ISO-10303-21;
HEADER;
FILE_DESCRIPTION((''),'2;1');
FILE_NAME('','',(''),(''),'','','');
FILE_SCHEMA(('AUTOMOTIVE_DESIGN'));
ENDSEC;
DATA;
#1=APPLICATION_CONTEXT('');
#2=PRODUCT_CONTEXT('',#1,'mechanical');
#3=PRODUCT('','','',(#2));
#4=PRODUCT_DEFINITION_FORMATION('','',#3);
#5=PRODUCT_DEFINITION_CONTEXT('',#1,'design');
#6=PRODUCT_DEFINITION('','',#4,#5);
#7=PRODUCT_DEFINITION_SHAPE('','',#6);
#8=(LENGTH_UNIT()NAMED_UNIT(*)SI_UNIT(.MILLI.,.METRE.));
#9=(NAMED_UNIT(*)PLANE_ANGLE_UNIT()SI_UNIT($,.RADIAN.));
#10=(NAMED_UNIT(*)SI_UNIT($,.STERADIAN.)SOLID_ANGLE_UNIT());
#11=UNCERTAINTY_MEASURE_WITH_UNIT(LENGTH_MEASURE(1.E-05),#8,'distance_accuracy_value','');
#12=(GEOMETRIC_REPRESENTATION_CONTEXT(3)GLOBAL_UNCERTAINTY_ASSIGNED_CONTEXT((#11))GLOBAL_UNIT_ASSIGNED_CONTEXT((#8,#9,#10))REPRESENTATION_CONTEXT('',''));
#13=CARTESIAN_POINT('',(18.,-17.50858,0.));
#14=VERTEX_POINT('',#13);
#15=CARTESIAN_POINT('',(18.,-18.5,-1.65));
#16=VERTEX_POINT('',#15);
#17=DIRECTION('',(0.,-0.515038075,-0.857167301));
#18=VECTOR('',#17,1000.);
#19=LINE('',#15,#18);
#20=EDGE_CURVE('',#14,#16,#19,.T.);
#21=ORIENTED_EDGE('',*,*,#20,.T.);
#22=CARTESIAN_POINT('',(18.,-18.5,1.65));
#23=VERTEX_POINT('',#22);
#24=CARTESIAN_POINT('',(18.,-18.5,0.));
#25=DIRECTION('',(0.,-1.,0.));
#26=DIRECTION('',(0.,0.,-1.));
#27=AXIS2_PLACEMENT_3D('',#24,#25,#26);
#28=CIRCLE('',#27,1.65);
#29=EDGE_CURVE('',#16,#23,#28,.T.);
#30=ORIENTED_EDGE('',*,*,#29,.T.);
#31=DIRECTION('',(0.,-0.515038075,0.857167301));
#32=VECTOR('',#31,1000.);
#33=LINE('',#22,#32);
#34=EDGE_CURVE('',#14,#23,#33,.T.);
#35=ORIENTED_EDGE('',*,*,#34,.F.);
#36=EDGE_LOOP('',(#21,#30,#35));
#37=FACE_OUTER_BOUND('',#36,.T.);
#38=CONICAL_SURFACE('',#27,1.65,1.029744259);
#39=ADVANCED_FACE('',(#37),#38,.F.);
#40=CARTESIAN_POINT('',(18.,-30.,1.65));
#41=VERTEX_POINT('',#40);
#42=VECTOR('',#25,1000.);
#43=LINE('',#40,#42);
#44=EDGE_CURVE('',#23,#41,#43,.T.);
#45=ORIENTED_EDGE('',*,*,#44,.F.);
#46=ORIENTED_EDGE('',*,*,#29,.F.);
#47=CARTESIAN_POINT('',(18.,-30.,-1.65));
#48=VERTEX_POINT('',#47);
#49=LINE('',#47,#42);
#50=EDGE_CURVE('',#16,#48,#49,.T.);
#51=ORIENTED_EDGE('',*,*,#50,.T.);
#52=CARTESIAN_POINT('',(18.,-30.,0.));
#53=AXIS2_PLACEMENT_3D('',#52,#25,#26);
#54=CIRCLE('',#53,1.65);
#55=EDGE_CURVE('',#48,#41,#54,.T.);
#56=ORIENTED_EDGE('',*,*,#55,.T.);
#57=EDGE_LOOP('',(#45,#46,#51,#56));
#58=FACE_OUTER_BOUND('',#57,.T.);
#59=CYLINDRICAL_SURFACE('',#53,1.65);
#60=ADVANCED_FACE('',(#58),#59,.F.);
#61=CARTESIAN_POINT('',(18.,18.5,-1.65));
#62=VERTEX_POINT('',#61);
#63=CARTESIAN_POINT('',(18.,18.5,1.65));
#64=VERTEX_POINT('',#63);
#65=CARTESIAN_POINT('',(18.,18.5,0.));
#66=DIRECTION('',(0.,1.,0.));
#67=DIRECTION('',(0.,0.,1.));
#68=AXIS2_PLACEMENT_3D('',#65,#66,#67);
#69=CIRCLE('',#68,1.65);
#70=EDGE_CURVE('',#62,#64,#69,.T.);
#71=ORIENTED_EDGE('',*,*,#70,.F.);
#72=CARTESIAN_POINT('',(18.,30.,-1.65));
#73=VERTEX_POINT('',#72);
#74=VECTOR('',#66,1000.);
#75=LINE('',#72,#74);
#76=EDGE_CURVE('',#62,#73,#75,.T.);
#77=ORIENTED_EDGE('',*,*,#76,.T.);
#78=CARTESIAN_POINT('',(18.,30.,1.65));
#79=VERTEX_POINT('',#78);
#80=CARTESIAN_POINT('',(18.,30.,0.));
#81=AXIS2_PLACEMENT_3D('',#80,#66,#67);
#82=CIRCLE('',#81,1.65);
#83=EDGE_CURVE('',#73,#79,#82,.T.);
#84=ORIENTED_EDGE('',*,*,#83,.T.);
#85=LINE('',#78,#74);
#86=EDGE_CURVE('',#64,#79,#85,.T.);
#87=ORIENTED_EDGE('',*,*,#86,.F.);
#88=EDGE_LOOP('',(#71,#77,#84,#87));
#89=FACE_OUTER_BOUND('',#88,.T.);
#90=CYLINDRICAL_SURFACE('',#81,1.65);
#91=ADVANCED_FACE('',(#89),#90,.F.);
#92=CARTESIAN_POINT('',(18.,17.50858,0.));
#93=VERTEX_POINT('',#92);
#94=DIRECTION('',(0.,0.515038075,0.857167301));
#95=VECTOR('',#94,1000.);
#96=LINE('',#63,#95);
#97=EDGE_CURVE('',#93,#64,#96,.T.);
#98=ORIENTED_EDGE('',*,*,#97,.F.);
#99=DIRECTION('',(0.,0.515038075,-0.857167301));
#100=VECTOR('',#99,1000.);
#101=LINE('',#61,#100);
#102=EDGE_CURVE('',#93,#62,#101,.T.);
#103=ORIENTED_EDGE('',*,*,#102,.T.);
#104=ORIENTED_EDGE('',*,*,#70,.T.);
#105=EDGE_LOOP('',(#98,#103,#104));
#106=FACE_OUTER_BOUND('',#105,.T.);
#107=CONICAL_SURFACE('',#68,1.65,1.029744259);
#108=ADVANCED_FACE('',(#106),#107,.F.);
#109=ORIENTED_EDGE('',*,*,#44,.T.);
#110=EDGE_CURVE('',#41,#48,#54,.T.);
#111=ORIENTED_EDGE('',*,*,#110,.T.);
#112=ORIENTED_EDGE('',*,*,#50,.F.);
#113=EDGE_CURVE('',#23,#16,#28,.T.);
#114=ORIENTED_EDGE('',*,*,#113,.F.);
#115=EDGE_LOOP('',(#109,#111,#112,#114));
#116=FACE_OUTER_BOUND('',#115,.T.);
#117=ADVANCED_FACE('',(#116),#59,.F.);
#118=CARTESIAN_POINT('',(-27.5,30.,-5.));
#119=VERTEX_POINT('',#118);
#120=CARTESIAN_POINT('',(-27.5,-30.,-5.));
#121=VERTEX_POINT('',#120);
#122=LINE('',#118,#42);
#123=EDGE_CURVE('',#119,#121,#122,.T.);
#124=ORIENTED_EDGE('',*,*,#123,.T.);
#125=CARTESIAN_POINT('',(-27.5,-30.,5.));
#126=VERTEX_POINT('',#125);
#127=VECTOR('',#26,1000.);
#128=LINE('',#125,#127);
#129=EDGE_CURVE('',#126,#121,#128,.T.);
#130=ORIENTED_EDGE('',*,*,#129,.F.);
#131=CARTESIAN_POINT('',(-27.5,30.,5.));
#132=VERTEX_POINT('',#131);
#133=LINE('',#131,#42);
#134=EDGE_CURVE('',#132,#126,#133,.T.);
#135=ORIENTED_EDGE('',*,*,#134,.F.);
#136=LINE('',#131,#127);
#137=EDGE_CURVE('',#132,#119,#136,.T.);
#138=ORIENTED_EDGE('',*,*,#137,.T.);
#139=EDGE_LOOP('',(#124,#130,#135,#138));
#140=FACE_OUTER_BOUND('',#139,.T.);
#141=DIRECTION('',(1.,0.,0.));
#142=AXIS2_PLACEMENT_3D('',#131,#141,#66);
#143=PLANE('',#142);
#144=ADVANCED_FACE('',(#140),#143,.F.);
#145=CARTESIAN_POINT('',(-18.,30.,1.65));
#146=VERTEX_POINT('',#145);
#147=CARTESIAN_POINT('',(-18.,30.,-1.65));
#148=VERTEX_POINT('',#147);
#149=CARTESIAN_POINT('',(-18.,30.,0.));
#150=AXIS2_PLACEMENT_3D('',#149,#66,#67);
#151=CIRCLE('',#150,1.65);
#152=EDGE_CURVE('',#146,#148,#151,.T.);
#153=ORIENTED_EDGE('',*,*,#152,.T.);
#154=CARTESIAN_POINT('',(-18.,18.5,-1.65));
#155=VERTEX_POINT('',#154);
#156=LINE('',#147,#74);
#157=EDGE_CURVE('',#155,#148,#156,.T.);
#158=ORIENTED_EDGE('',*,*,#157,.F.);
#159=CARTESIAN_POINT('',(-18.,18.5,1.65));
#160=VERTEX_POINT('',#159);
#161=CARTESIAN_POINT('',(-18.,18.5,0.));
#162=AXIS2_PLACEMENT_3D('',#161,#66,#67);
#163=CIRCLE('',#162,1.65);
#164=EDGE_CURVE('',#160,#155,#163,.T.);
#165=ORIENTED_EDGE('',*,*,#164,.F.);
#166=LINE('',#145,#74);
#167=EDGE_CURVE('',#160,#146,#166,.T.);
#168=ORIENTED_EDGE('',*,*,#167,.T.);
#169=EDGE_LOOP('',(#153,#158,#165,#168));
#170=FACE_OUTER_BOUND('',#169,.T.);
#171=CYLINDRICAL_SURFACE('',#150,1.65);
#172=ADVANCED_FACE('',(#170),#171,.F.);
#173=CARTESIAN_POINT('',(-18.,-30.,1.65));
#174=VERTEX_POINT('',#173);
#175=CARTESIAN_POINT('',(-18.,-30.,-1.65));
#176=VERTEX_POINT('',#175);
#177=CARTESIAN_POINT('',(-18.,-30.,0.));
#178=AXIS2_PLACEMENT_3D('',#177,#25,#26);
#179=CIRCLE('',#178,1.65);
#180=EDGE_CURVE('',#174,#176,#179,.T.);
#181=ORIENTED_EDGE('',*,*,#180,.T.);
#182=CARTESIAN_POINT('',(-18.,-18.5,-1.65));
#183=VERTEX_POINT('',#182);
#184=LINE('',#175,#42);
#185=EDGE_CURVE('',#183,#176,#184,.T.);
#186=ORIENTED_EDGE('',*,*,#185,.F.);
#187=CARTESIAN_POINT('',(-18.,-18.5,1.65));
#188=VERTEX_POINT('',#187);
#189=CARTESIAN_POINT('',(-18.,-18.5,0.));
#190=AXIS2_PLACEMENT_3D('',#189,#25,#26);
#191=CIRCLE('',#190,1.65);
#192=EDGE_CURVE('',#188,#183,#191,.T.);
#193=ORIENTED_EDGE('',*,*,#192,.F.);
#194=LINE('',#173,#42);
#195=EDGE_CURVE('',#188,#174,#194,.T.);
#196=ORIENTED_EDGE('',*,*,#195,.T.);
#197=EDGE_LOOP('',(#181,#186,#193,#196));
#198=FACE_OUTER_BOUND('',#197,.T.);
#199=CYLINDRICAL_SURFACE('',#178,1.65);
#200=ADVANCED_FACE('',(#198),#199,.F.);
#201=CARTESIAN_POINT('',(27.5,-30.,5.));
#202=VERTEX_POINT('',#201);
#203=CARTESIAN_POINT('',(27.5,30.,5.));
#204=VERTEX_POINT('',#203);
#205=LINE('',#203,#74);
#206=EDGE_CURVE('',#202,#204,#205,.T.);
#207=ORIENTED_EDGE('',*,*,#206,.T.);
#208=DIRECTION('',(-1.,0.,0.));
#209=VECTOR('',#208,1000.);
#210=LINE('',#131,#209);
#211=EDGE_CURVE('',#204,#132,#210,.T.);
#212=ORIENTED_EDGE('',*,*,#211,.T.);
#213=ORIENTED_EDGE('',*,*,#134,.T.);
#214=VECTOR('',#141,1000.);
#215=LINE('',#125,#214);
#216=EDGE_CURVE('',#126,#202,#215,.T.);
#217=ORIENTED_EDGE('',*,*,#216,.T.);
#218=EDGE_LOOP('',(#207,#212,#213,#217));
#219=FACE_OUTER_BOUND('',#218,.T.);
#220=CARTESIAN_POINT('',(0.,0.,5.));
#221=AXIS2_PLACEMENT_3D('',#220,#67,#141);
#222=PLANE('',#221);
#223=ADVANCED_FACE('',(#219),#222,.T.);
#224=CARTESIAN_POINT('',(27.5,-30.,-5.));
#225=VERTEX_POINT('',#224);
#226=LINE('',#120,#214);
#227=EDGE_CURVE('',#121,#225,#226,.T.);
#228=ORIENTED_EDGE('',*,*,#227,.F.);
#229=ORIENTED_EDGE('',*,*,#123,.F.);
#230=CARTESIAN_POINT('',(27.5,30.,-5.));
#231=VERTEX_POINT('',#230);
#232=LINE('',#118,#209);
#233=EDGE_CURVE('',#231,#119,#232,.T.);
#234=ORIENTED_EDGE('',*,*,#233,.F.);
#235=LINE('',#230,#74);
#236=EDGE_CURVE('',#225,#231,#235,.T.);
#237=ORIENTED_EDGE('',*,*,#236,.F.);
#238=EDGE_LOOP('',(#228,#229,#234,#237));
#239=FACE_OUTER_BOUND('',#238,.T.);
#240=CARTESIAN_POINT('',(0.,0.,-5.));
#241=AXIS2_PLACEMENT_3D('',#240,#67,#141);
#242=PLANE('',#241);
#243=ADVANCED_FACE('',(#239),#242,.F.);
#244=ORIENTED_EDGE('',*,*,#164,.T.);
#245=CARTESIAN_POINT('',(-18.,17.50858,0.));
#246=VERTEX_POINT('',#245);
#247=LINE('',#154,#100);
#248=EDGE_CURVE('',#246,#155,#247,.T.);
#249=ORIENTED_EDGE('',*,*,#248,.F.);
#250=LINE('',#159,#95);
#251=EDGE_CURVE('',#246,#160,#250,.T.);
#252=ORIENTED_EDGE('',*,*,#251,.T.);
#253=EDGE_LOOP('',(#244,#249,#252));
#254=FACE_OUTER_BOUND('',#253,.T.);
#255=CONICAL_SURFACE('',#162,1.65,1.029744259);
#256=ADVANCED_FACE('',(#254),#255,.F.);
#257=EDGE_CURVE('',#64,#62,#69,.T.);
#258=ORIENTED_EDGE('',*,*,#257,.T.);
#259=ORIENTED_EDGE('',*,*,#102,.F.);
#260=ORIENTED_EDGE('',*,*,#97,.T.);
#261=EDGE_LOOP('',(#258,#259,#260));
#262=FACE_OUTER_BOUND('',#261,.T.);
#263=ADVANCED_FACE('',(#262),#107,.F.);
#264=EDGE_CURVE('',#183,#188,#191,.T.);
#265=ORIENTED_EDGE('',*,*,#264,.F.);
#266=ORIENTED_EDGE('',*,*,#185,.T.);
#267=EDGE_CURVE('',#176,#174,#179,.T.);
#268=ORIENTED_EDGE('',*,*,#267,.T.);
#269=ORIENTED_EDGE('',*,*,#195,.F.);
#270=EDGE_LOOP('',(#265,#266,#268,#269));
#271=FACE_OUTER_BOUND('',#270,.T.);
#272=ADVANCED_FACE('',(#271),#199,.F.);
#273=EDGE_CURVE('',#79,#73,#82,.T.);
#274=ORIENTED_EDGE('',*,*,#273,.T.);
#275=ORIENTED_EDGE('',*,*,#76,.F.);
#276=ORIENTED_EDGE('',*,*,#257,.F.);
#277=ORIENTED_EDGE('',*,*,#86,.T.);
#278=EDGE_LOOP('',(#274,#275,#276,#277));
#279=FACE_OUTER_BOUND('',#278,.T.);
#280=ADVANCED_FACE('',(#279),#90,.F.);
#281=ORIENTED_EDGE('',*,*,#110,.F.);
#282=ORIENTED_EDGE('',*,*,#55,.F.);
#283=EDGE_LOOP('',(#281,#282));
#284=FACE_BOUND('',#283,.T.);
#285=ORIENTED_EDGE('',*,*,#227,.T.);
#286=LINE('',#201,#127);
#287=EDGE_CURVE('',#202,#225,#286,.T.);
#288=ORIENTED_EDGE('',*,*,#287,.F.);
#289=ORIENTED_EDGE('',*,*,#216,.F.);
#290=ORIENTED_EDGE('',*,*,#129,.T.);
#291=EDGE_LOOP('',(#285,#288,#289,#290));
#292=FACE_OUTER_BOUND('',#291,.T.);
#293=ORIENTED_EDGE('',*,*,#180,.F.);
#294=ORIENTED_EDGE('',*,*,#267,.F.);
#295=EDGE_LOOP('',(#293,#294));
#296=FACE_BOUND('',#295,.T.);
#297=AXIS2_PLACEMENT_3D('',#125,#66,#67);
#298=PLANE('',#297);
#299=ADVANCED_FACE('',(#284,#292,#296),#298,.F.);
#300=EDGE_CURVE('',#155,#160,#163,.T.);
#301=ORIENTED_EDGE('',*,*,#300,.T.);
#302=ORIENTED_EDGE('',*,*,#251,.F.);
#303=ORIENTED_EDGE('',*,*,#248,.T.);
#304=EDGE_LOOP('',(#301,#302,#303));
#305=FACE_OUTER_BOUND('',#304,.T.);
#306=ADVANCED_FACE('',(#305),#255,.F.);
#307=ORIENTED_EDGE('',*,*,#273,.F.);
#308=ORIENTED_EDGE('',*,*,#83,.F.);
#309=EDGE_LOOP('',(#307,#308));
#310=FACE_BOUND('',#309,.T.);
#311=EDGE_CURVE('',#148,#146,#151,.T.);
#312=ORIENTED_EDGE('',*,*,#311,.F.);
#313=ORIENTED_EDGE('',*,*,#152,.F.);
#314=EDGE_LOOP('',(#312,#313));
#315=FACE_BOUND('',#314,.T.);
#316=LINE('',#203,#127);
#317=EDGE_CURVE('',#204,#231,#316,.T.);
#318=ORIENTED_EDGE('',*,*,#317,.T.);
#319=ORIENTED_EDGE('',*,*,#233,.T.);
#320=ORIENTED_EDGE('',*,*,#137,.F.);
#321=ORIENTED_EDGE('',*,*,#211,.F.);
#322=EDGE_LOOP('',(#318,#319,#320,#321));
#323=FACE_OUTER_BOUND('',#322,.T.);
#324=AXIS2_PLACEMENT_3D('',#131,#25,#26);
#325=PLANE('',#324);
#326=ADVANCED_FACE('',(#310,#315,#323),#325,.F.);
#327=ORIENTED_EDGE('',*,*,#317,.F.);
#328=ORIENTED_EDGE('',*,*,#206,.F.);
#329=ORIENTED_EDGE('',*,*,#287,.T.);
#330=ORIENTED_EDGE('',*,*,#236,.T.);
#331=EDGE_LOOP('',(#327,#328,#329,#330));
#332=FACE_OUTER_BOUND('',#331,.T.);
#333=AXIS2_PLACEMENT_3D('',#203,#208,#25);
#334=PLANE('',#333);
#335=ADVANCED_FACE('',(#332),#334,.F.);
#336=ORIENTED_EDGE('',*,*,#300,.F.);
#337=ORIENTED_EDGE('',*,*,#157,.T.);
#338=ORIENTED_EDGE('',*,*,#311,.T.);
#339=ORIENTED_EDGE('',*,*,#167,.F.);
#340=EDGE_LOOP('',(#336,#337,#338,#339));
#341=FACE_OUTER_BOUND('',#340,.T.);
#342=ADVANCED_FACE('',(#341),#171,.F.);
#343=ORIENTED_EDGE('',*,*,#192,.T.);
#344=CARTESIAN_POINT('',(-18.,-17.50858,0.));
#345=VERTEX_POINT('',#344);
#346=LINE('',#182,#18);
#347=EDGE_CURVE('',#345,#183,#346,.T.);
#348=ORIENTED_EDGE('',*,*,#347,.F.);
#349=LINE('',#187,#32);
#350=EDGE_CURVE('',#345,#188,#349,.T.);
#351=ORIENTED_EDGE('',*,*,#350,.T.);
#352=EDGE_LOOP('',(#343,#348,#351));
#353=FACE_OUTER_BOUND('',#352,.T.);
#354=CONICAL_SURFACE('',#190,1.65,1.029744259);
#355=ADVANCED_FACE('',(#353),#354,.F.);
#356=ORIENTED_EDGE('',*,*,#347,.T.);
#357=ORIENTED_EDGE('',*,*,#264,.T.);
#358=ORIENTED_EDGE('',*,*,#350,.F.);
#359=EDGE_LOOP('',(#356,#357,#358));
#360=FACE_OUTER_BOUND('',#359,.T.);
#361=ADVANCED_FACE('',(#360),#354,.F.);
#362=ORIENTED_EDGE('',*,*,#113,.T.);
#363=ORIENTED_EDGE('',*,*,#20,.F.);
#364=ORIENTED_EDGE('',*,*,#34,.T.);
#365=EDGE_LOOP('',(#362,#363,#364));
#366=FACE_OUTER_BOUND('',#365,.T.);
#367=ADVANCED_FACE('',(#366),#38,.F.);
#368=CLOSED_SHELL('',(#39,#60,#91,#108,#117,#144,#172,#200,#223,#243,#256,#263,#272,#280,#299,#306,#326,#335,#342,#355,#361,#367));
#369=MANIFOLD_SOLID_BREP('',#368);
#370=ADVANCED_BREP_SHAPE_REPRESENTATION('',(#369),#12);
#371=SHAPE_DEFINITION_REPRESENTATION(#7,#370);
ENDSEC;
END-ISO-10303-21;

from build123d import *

# Parameters (mm, degrees)
SKETCH_1_W                  = 55
SKETCH_1_H                  = 60
EXTRUDE_1_DEPTH             = 5
HOLE_WIZARD_M4_1_AT_2_COUNT = 2
HOLE_WIZARD_M4_1_AT_2_PITCH = 36


with BuildPart() as part:
    # 草图1 → 凸台-拉伸1 (new, symmetric)
    with BuildSketch(Plane.XY):
        Rectangle(SKETCH_1_W, SKETCH_1_H)
    extrude(amount=EXTRUDE_1_DEPTH, both=True)

    # 草图4 → M4 螺纹孔1 (revolve, cut)
    with BuildSketch(Plane(origin=(18, -30, 0), x_dir=(0, 0, -1), z_dir=(1, 0, 0))):
        Polygon((0, 0), (0, 12.491420021), (1.65, 11.5), (1.65, 0), align=None)
    hole_wizard_m4_1 = revolve(axis=Axis((18, -36.35, 0), (0, 1, 0)), mode=Mode.SUBTRACT)

    # M4 螺纹孔1 at 2: M4 螺纹孔1 ×2
    with Locations(*[(-i * HOLE_WIZARD_M4_1_AT_2_PITCH, 0, 0) for i in range(1, HOLE_WIZARD_M4_1_AT_2_COUNT)]):
        add(hole_wizard_m4_1, mode=Mode.SUBTRACT)

    # 镜向1: M4 螺纹孔1 across plane
    add(hole_wizard_m4_1.mirror(Plane.ZX), mode=Mode.SUBTRACT)

    # 镜向1 copy 1 sketch → 镜向1 copy 1 (revolve, cut)
    with BuildSketch(Plane(origin=(-18, 30, 0), x_dir=(0, 0, -1), z_dir=(1, 0, 0))):
        Polygon((0, 0), (0, -12.491420021), (1.65, -11.5), (1.65, 0), align=None)
    revolve(axis=Axis((-18, 36.35, 0), (0, 1, 0)), mode=Mode.SUBTRACT)


solid = part.part
